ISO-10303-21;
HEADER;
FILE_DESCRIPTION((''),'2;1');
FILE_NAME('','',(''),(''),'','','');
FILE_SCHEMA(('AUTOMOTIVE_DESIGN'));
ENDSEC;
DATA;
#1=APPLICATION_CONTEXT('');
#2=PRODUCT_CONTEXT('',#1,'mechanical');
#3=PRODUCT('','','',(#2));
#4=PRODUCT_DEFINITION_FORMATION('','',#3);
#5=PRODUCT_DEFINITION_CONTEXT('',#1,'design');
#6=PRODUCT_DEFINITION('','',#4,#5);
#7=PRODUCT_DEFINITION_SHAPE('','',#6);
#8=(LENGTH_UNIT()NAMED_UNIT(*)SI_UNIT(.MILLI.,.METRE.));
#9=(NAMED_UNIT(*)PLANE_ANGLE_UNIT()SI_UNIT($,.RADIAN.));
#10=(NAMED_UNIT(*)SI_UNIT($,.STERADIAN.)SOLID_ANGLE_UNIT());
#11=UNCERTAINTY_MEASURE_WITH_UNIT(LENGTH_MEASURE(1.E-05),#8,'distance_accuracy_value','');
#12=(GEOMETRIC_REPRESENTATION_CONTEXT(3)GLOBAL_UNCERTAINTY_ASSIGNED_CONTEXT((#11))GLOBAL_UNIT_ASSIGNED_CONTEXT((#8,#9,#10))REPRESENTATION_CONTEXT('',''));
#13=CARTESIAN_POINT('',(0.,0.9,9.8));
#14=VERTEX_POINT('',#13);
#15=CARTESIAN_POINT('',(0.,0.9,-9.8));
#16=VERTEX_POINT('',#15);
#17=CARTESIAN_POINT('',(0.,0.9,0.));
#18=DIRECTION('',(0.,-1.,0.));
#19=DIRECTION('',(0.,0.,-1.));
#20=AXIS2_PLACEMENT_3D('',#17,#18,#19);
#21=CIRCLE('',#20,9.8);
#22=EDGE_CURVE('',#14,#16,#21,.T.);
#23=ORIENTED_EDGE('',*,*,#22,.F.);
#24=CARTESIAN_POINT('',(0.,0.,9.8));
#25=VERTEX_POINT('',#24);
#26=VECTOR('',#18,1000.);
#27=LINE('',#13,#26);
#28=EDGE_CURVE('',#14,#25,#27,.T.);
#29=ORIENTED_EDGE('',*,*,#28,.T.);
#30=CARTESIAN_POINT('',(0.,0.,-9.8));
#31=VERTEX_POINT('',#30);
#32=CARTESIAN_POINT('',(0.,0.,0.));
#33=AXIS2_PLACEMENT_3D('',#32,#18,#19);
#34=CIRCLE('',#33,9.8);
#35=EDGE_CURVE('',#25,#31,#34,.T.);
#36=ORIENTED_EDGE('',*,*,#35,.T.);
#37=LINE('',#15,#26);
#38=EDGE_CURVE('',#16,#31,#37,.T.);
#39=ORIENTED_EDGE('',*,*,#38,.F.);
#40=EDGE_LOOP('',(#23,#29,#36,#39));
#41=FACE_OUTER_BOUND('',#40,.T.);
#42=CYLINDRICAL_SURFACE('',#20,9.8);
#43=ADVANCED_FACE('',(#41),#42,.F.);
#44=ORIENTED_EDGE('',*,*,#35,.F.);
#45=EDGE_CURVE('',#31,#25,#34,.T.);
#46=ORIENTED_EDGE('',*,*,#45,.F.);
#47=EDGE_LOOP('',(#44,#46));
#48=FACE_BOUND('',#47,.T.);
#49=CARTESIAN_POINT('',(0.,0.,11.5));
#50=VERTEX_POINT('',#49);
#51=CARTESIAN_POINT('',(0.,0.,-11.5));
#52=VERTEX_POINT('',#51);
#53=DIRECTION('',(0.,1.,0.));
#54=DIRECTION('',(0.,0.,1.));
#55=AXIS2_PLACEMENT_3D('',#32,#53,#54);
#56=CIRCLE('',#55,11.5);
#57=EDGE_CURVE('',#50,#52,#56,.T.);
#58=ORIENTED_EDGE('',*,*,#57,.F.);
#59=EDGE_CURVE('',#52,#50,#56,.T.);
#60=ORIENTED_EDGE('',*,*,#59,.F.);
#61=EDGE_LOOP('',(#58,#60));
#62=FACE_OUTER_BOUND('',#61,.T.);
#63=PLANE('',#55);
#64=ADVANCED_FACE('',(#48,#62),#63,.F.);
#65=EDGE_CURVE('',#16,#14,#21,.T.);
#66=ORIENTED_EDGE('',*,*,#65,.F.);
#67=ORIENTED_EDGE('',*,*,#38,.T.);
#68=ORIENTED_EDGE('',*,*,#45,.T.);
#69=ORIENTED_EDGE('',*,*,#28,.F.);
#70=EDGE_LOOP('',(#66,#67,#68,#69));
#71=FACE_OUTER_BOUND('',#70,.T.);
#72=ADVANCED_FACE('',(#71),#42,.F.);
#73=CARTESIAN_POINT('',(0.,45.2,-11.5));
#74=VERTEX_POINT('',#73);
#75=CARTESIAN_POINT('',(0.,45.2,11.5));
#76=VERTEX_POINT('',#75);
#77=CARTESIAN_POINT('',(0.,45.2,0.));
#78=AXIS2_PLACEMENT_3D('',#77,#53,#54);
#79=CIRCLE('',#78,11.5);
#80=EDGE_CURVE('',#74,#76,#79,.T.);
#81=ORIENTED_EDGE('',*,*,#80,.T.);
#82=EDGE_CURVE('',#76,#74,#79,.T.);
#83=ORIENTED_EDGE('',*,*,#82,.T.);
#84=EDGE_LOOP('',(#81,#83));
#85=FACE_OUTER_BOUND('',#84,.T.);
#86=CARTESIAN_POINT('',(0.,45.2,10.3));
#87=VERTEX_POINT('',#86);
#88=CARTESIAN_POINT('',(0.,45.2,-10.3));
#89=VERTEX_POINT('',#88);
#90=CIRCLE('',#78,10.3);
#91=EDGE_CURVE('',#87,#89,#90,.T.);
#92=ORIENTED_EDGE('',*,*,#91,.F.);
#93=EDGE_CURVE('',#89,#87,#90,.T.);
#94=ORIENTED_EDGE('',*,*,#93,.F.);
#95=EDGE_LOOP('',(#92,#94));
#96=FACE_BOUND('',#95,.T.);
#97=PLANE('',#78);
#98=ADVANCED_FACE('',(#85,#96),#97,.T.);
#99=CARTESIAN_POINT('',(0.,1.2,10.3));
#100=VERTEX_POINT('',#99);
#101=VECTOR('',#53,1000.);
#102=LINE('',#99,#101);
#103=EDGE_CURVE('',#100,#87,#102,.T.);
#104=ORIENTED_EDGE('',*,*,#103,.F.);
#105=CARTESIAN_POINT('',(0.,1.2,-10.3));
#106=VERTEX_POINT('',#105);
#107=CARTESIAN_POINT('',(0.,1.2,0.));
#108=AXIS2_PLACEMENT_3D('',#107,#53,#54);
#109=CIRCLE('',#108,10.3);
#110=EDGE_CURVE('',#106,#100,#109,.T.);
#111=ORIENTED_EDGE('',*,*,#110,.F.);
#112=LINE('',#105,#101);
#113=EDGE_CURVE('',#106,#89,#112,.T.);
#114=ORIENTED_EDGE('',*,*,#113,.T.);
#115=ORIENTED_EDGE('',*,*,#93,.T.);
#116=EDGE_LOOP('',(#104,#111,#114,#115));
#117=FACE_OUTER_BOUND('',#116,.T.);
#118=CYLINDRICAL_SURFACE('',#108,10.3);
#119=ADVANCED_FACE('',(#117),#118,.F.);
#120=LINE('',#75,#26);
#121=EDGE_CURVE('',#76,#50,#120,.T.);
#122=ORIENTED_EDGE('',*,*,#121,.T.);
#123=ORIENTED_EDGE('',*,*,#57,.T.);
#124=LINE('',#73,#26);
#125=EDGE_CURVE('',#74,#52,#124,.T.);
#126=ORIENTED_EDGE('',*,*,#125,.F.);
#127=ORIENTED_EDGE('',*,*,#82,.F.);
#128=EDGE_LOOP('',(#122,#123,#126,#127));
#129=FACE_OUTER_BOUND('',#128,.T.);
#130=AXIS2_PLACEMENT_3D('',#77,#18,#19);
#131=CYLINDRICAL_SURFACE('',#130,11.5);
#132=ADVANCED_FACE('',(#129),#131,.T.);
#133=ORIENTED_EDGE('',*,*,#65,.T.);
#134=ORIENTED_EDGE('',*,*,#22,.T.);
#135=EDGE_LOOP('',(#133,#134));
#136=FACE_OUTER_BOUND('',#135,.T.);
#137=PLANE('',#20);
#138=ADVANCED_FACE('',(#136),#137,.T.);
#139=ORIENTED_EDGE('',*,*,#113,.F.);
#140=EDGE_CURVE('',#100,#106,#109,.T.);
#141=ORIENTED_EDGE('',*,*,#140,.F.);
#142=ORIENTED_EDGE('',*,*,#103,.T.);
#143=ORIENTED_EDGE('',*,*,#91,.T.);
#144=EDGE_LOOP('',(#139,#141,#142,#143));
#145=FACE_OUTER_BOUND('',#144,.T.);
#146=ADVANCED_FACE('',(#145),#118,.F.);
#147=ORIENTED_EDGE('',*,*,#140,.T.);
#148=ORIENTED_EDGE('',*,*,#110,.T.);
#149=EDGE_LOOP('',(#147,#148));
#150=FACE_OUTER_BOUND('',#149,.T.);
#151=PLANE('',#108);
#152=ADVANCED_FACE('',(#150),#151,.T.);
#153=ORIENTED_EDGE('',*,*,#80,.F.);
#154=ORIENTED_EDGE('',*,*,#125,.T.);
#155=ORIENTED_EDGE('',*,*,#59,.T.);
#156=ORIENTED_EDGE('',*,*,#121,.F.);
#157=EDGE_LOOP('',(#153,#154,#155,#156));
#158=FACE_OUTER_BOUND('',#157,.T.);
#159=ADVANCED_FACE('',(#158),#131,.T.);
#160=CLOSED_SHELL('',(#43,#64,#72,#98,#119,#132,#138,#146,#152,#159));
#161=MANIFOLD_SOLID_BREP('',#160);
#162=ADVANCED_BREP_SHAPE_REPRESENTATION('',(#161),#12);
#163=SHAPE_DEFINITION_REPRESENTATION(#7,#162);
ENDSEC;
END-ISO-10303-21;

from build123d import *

# Parameters (mm, degrees)
SKETCH1_R           = 11.5
BOSS_EXTRUDE1_DEPTH = 45.2
SKETCH4_R           = 10.3
CUT_EXTRUDE1_DEPTH  = 44
SKETCH5_R           = 9.8
CUT_EXTRUDE2_DEPTH  = 0.9


with BuildPart() as part:
    # Sketch1 → Boss-Extrude1 (new body)
    with BuildSketch(Plane(origin=(0, 0, 0), x_dir=(1, 0, 0), z_dir=(0, 1, 0))):
        with Locations(Location((0, 0, 0), (0, 0, 270))):
            Circle(SKETCH1_R)
    extrude(amount=BOSS_EXTRUDE1_DEPTH)

    # Sketch4 → Cut-Extrude1 (cut)
    with BuildSketch(Plane(origin=(0, 45.2, 0), x_dir=(1, 0, 0), z_dir=(0, 1, 0))):
        with Locations(Location((0, 0, 0), (0, 0, 270))):
            Circle(SKETCH4_R)
    extrude(amount=-CUT_EXTRUDE1_DEPTH, mode=Mode.SUBTRACT)

    # Sketch5 → Cut-Extrude2 (cut)
    with BuildSketch(Plane.XZ):
        with Locations(Location((0, 0, 0), (0, 0, 270))):
            Circle(SKETCH5_R)
    extrude(amount=-CUT_EXTRUDE2_DEPTH, mode=Mode.SUBTRACT)


solid = part.part
